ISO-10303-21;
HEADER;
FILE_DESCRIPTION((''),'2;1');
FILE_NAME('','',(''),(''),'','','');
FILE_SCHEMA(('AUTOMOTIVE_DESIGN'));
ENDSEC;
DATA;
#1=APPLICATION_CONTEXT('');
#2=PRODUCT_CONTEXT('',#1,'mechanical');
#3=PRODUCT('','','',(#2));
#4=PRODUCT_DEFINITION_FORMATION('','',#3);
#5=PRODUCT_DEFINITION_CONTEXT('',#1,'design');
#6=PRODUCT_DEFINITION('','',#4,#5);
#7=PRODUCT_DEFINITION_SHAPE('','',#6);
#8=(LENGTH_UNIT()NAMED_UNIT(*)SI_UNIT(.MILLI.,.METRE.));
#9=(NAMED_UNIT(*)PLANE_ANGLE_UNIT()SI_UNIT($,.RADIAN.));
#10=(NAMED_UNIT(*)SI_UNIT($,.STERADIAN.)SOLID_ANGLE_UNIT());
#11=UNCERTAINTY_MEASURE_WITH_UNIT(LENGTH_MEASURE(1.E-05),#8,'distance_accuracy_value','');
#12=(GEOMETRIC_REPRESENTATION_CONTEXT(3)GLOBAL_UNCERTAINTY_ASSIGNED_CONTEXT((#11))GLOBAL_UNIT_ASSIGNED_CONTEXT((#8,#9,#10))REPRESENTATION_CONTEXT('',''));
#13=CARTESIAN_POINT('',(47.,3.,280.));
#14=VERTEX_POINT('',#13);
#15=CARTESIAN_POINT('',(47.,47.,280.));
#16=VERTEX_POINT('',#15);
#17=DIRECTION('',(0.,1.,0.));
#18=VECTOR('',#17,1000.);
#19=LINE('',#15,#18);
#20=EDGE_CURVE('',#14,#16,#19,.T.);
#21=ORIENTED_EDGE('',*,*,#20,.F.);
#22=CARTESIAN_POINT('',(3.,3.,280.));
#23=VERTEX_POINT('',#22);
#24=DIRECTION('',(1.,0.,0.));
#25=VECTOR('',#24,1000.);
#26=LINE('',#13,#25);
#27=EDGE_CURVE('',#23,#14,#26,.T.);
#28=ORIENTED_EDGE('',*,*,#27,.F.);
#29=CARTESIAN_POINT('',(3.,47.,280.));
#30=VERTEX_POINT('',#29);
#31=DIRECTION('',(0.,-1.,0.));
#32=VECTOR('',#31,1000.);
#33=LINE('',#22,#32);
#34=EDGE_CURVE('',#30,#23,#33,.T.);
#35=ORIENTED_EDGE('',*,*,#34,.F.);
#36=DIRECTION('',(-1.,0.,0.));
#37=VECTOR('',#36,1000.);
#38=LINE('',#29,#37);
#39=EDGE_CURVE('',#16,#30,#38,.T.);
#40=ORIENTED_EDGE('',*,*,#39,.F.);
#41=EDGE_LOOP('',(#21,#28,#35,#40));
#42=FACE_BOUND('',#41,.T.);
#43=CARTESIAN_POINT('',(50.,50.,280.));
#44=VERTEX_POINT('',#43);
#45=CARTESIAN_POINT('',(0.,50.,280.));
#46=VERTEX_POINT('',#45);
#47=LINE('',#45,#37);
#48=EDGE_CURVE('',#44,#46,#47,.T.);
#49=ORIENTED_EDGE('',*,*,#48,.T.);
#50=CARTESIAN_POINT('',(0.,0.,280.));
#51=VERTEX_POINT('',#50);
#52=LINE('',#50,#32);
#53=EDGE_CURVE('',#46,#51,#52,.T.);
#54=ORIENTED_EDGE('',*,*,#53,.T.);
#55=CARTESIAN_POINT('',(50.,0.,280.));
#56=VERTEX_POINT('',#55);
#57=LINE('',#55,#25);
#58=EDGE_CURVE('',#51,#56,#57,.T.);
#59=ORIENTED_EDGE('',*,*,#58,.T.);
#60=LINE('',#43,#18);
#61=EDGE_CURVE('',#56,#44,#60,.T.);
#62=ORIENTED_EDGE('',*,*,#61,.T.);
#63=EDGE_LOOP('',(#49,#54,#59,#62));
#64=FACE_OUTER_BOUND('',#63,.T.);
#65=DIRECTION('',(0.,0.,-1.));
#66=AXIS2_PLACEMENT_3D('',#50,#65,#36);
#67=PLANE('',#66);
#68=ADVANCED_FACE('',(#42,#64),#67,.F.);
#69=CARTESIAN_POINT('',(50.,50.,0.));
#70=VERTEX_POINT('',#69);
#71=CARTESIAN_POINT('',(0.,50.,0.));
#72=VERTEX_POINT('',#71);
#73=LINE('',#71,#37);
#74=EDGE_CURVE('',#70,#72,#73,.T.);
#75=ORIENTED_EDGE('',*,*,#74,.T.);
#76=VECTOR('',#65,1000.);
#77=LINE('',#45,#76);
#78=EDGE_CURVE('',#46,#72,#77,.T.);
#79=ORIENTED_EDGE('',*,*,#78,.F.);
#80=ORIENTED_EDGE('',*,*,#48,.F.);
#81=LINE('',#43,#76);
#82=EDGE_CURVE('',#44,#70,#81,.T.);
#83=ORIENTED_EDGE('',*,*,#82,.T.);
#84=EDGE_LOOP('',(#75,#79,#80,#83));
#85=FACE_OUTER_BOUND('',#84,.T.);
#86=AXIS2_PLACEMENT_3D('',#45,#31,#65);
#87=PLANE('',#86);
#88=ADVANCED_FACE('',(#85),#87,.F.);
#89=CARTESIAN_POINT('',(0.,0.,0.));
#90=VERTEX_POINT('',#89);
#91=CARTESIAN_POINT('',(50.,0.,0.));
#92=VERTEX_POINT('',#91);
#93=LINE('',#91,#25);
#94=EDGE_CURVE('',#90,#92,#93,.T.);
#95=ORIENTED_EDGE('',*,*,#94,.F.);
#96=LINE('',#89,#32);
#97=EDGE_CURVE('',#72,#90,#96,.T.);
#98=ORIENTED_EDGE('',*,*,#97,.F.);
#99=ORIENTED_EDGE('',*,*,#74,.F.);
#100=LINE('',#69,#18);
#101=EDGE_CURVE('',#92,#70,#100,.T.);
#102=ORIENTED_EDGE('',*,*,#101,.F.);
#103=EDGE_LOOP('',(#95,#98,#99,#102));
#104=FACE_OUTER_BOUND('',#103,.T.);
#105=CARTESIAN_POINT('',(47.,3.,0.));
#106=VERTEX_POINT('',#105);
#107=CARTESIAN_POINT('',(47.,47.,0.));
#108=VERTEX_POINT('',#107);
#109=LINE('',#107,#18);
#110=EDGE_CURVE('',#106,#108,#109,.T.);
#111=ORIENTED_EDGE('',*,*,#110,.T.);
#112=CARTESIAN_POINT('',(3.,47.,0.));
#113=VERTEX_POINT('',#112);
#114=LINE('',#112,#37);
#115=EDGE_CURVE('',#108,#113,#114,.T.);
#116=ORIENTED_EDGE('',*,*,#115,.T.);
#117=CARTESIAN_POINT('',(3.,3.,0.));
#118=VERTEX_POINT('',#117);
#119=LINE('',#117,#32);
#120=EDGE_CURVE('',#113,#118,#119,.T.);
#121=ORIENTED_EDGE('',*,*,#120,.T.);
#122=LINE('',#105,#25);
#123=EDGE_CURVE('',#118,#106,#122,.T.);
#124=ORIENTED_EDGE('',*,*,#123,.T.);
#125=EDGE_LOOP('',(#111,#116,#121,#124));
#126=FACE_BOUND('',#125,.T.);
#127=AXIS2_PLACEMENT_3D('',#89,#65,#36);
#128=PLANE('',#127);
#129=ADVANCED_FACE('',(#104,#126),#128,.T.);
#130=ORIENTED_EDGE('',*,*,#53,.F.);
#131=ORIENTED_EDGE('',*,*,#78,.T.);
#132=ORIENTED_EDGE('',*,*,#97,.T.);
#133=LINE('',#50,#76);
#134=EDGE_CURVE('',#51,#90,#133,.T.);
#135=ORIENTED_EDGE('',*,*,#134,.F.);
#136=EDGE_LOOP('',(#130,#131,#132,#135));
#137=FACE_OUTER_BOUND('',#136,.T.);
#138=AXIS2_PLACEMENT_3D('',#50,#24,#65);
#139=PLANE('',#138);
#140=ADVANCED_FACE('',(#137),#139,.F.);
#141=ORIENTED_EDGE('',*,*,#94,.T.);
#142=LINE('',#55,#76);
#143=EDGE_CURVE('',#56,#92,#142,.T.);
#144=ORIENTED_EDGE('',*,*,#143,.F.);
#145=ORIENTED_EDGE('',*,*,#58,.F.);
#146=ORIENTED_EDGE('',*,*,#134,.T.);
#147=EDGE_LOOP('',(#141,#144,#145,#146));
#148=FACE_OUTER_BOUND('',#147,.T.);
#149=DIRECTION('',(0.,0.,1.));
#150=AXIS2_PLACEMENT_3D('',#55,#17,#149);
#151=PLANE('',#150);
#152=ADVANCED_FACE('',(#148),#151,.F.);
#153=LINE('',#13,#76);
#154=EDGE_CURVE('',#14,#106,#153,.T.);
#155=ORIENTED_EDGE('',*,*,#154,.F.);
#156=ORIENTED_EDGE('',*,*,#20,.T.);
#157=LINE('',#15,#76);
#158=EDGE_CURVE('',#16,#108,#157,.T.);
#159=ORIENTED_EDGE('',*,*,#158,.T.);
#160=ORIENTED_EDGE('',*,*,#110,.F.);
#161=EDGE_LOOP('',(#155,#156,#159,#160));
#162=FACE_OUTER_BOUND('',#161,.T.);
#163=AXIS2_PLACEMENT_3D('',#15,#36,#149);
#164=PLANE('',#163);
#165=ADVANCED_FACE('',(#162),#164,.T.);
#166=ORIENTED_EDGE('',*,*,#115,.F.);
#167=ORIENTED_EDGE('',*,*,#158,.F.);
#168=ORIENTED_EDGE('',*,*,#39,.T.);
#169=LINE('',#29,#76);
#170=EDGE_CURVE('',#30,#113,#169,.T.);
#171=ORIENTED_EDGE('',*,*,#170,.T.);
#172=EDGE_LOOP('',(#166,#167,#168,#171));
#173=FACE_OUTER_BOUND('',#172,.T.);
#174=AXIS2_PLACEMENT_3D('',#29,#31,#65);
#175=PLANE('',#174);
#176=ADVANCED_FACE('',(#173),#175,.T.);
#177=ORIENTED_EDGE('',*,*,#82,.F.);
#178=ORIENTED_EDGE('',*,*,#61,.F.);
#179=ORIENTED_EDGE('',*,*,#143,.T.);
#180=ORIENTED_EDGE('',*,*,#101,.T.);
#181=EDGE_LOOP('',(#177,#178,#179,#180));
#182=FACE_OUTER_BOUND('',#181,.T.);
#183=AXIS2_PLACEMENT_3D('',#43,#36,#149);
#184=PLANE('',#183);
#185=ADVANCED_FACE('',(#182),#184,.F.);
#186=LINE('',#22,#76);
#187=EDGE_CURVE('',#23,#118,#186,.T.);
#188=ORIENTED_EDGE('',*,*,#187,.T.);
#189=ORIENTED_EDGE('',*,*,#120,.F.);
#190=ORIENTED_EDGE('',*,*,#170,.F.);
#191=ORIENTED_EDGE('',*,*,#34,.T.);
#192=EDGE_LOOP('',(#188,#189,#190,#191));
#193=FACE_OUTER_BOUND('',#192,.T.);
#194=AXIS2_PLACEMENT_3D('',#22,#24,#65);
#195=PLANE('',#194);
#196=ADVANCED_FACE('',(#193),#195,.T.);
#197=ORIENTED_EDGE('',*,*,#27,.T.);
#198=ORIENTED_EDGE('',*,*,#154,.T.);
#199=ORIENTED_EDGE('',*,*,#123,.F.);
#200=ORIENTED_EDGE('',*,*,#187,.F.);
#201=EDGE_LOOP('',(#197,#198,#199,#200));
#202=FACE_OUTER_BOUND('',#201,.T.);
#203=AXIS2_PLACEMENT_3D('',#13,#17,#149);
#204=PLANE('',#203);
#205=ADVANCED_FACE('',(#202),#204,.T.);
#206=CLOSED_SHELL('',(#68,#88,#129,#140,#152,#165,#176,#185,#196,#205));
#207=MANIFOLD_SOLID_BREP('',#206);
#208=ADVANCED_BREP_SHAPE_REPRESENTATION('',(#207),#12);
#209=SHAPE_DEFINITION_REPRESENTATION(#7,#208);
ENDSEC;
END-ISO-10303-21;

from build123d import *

# Parameters (mm, degrees)
SKETCH_1_W      = 50
SKETCH_1_H      = 50
SKETCH_1_W_2    = 44
SKETCH_1_H_2    = 44
EXTRUDE_2_DEPTH = 280


with BuildPart() as part:
    # 草图1 → 凸台-拉伸2 (new body)
    with BuildSketch(Plane.XY):
        with Locations((25, 25)):
            Rectangle(SKETCH_1_W, SKETCH_1_H)
        with Locations((25, 25)):
            Rectangle(SKETCH_1_W_2, SKETCH_1_H_2, mode=Mode.SUBTRACT)
    extrude(amount=EXTRUDE_2_DEPTH)


solid = part.part
